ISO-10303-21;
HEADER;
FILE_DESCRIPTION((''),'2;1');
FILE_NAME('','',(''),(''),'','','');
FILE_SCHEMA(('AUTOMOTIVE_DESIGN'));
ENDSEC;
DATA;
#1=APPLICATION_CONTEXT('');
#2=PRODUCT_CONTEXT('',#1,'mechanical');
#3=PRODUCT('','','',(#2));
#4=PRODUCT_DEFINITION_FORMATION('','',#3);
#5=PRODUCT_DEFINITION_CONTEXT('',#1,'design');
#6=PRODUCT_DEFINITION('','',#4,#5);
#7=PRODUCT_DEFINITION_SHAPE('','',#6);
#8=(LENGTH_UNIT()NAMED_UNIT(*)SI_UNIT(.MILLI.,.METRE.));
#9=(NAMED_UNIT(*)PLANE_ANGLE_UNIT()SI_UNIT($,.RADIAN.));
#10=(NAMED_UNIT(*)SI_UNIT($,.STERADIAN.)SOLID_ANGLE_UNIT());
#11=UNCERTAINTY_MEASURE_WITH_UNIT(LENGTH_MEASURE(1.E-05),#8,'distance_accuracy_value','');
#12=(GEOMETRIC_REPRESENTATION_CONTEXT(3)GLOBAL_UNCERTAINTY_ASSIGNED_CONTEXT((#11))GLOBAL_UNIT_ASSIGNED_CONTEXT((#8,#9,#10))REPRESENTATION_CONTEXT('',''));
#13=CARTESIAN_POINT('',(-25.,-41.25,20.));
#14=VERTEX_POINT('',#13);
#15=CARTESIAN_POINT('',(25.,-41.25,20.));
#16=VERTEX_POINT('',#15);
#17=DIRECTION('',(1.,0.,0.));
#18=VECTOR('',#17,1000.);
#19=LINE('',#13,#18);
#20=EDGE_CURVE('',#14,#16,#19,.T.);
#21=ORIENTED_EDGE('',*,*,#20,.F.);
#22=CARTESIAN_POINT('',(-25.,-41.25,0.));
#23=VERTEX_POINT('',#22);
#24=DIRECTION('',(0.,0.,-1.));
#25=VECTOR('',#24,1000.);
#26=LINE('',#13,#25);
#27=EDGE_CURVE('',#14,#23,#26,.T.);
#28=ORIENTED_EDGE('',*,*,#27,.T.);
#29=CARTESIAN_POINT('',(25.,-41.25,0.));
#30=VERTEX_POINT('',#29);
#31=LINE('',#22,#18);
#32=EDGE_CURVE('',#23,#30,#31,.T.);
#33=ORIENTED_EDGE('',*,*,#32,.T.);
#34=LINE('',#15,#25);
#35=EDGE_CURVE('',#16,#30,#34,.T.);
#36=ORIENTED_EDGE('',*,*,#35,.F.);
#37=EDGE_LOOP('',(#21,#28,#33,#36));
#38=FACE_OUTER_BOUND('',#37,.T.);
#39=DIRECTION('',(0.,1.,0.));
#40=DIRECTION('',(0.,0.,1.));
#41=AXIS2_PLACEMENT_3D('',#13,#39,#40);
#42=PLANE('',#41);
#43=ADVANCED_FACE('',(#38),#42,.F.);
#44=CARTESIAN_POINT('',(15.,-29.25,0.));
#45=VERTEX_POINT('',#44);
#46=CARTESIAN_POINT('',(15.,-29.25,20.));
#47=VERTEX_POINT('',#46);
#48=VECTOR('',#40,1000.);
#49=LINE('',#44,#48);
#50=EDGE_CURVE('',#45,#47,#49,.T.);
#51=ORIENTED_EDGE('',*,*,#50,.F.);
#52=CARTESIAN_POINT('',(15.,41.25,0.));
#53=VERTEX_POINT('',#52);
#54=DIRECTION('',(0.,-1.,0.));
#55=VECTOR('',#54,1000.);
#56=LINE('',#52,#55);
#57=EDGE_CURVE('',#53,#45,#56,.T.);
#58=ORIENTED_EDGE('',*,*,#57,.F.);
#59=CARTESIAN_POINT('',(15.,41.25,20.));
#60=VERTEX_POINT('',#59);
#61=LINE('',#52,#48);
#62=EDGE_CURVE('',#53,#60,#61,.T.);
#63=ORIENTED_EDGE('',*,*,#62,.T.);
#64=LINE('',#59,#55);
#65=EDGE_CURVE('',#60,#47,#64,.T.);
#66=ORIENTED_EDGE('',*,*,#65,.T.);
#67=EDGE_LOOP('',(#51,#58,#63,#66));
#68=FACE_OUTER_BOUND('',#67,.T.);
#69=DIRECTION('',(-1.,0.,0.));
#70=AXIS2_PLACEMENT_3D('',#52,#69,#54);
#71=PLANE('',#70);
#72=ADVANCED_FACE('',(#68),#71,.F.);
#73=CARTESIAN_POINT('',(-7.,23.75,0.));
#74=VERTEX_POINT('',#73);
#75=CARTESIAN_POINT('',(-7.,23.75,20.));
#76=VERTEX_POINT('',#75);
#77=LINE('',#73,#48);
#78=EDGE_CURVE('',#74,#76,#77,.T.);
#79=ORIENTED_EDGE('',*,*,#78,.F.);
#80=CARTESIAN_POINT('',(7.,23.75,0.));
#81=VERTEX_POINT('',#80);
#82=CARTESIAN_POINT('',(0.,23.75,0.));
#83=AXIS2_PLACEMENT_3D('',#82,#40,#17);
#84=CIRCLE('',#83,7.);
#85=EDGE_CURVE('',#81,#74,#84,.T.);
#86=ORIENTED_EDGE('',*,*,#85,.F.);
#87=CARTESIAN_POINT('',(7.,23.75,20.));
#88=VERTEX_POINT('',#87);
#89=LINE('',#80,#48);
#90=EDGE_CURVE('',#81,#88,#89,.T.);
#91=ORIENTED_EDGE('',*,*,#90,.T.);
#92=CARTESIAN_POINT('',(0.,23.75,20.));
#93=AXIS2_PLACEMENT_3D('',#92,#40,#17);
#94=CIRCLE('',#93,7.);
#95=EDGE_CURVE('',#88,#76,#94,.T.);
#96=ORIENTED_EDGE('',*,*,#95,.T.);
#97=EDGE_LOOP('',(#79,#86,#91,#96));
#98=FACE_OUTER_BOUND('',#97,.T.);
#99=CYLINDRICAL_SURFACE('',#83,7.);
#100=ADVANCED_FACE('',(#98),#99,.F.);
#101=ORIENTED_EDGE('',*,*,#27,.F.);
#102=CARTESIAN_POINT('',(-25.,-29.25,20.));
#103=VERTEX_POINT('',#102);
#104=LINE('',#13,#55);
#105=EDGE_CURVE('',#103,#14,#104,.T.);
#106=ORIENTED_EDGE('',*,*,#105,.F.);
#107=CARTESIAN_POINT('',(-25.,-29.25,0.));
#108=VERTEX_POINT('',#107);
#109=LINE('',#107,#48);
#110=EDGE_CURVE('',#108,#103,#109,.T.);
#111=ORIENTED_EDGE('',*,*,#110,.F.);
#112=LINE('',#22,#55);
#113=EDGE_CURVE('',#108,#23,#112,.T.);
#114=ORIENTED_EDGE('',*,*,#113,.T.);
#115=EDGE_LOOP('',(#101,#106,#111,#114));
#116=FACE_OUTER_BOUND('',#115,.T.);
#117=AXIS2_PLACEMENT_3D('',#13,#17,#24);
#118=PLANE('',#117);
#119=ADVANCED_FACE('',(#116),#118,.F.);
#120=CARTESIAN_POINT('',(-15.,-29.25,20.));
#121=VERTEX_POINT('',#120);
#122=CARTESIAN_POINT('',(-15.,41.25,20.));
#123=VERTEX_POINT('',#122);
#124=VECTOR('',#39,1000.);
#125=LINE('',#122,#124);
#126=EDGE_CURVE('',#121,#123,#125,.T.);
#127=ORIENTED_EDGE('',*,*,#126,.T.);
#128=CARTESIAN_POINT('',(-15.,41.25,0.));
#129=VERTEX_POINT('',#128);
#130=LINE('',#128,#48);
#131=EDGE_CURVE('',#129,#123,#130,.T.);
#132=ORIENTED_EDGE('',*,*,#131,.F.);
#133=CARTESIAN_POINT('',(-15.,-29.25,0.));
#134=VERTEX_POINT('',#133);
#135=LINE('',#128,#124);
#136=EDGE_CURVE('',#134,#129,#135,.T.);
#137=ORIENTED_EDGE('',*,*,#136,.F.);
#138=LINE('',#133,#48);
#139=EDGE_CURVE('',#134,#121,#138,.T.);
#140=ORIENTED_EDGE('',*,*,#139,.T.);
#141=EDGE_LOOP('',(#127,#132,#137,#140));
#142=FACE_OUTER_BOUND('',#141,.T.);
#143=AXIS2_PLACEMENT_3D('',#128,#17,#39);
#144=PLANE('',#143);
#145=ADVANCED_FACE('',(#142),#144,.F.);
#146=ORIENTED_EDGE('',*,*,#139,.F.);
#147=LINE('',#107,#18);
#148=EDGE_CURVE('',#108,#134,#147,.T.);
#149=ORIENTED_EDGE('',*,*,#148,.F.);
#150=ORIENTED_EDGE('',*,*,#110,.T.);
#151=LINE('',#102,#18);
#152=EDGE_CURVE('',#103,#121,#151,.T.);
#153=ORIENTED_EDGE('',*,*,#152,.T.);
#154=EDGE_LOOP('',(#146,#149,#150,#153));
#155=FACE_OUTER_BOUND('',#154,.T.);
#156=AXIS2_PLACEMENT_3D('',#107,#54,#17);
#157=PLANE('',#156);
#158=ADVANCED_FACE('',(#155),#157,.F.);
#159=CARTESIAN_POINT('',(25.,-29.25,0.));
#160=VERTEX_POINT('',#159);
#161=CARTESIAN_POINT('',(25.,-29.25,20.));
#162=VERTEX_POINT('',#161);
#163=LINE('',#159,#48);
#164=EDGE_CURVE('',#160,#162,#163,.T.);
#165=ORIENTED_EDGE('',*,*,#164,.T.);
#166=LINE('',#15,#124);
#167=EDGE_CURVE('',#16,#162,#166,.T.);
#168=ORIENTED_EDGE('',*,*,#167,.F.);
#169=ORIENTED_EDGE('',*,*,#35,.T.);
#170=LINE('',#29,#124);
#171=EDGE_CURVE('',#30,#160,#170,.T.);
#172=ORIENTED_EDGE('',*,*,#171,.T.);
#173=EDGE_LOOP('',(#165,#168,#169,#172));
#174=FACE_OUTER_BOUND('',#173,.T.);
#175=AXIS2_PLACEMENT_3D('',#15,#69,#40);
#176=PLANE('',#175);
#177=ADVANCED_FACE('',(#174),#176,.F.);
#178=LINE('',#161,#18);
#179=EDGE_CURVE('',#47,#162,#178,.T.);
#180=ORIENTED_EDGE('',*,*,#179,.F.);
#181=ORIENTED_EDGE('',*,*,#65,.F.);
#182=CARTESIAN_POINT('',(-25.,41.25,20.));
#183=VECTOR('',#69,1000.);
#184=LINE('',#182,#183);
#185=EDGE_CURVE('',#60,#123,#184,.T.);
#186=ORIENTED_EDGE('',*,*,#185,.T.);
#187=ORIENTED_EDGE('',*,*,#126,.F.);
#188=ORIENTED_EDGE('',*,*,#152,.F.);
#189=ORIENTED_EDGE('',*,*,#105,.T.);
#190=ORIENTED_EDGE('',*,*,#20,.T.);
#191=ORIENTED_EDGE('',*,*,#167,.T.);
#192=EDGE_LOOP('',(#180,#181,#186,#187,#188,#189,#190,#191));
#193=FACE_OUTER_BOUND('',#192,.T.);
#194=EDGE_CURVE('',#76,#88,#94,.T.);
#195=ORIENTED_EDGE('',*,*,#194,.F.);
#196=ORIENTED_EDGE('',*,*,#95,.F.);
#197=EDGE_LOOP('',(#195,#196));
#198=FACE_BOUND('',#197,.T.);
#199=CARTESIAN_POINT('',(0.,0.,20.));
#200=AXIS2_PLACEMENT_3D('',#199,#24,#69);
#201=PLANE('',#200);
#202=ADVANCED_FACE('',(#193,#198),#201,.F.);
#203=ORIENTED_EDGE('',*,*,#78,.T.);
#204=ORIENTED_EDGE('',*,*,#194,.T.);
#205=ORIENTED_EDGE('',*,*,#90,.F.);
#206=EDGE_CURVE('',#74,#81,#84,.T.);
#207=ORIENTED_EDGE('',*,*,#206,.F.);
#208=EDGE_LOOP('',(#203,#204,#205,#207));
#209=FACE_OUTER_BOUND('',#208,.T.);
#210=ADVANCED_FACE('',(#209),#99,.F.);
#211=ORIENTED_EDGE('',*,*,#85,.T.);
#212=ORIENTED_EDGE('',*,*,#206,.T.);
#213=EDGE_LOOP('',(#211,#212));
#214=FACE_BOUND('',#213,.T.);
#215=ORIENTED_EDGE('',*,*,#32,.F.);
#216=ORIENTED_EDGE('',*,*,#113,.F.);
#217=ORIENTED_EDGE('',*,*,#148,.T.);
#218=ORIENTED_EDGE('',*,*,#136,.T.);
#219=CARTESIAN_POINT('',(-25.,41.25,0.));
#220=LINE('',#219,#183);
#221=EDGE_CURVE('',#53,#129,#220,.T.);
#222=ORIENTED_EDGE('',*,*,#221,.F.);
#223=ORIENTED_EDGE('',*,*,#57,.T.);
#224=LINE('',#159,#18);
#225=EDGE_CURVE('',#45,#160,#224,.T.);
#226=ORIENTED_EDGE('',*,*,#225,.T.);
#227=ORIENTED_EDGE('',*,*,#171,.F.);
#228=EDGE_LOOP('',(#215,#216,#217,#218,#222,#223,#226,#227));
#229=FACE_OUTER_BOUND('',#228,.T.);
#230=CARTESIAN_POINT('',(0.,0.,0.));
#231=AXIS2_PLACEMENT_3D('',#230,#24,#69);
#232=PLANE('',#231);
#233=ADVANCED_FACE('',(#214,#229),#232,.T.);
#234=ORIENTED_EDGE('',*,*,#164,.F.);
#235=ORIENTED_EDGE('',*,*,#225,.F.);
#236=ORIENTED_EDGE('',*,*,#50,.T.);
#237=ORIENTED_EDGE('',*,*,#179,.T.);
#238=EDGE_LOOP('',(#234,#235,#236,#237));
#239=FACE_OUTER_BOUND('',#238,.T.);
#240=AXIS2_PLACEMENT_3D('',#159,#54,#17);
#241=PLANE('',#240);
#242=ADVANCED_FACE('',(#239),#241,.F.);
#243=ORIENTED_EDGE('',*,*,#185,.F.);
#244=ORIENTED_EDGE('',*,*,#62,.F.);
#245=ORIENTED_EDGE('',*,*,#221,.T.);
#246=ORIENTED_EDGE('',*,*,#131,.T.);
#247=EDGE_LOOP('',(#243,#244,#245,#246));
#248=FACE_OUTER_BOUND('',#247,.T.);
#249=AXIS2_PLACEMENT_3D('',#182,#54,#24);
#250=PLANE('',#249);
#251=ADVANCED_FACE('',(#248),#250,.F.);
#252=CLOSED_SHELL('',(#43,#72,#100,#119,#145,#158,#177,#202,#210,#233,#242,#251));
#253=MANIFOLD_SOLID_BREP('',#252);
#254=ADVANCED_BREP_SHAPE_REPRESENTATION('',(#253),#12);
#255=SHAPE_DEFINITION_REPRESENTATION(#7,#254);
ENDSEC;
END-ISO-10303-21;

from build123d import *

# Parameters (mm, degrees)
SKETCH_1_W          = 50
SKETCH_1_H          = 82.5
EXTRUDE_1_DEPTH     = 20
SKETCH_2_R          = 7
CUT_EXTRUDE_1_DEPTH = 53.216496436
SKETCH_3_W          = 10
SKETCH_3_H          = 70.5
CUT_EXTRUDE_2_DEPTH = 53.216496436


with BuildPart() as part:
    # 草图1 → 凸台-拉伸1 (new body)
    with BuildSketch(Plane.XY):
        Rectangle(SKETCH_1_W, SKETCH_1_H)
    extrude(amount=EXTRUDE_1_DEPTH)

    # 草图2 → 切除-拉伸1 (cut, through all)
    with BuildSketch(Plane.XY.offset(20)):
        with Locations((0, 23.75)):
            Circle(SKETCH_2_R)
    extrude(amount=-CUT_EXTRUDE_1_DEPTH, mode=Mode.SUBTRACT)

    # 草图3 → 切除-拉伸2 (cut, through all)
    with BuildSketch(Plane.XY.offset(20)):
        with Locations((-20, 6)):
            Rectangle(SKETCH_3_W, SKETCH_3_H)
        with Locations((20, 6)):
            Rectangle(SKETCH_3_W, SKETCH_3_H)
    extrude(amount=-CUT_EXTRUDE_2_DEPTH, mode=Mode.SUBTRACT)


solid = part.part
